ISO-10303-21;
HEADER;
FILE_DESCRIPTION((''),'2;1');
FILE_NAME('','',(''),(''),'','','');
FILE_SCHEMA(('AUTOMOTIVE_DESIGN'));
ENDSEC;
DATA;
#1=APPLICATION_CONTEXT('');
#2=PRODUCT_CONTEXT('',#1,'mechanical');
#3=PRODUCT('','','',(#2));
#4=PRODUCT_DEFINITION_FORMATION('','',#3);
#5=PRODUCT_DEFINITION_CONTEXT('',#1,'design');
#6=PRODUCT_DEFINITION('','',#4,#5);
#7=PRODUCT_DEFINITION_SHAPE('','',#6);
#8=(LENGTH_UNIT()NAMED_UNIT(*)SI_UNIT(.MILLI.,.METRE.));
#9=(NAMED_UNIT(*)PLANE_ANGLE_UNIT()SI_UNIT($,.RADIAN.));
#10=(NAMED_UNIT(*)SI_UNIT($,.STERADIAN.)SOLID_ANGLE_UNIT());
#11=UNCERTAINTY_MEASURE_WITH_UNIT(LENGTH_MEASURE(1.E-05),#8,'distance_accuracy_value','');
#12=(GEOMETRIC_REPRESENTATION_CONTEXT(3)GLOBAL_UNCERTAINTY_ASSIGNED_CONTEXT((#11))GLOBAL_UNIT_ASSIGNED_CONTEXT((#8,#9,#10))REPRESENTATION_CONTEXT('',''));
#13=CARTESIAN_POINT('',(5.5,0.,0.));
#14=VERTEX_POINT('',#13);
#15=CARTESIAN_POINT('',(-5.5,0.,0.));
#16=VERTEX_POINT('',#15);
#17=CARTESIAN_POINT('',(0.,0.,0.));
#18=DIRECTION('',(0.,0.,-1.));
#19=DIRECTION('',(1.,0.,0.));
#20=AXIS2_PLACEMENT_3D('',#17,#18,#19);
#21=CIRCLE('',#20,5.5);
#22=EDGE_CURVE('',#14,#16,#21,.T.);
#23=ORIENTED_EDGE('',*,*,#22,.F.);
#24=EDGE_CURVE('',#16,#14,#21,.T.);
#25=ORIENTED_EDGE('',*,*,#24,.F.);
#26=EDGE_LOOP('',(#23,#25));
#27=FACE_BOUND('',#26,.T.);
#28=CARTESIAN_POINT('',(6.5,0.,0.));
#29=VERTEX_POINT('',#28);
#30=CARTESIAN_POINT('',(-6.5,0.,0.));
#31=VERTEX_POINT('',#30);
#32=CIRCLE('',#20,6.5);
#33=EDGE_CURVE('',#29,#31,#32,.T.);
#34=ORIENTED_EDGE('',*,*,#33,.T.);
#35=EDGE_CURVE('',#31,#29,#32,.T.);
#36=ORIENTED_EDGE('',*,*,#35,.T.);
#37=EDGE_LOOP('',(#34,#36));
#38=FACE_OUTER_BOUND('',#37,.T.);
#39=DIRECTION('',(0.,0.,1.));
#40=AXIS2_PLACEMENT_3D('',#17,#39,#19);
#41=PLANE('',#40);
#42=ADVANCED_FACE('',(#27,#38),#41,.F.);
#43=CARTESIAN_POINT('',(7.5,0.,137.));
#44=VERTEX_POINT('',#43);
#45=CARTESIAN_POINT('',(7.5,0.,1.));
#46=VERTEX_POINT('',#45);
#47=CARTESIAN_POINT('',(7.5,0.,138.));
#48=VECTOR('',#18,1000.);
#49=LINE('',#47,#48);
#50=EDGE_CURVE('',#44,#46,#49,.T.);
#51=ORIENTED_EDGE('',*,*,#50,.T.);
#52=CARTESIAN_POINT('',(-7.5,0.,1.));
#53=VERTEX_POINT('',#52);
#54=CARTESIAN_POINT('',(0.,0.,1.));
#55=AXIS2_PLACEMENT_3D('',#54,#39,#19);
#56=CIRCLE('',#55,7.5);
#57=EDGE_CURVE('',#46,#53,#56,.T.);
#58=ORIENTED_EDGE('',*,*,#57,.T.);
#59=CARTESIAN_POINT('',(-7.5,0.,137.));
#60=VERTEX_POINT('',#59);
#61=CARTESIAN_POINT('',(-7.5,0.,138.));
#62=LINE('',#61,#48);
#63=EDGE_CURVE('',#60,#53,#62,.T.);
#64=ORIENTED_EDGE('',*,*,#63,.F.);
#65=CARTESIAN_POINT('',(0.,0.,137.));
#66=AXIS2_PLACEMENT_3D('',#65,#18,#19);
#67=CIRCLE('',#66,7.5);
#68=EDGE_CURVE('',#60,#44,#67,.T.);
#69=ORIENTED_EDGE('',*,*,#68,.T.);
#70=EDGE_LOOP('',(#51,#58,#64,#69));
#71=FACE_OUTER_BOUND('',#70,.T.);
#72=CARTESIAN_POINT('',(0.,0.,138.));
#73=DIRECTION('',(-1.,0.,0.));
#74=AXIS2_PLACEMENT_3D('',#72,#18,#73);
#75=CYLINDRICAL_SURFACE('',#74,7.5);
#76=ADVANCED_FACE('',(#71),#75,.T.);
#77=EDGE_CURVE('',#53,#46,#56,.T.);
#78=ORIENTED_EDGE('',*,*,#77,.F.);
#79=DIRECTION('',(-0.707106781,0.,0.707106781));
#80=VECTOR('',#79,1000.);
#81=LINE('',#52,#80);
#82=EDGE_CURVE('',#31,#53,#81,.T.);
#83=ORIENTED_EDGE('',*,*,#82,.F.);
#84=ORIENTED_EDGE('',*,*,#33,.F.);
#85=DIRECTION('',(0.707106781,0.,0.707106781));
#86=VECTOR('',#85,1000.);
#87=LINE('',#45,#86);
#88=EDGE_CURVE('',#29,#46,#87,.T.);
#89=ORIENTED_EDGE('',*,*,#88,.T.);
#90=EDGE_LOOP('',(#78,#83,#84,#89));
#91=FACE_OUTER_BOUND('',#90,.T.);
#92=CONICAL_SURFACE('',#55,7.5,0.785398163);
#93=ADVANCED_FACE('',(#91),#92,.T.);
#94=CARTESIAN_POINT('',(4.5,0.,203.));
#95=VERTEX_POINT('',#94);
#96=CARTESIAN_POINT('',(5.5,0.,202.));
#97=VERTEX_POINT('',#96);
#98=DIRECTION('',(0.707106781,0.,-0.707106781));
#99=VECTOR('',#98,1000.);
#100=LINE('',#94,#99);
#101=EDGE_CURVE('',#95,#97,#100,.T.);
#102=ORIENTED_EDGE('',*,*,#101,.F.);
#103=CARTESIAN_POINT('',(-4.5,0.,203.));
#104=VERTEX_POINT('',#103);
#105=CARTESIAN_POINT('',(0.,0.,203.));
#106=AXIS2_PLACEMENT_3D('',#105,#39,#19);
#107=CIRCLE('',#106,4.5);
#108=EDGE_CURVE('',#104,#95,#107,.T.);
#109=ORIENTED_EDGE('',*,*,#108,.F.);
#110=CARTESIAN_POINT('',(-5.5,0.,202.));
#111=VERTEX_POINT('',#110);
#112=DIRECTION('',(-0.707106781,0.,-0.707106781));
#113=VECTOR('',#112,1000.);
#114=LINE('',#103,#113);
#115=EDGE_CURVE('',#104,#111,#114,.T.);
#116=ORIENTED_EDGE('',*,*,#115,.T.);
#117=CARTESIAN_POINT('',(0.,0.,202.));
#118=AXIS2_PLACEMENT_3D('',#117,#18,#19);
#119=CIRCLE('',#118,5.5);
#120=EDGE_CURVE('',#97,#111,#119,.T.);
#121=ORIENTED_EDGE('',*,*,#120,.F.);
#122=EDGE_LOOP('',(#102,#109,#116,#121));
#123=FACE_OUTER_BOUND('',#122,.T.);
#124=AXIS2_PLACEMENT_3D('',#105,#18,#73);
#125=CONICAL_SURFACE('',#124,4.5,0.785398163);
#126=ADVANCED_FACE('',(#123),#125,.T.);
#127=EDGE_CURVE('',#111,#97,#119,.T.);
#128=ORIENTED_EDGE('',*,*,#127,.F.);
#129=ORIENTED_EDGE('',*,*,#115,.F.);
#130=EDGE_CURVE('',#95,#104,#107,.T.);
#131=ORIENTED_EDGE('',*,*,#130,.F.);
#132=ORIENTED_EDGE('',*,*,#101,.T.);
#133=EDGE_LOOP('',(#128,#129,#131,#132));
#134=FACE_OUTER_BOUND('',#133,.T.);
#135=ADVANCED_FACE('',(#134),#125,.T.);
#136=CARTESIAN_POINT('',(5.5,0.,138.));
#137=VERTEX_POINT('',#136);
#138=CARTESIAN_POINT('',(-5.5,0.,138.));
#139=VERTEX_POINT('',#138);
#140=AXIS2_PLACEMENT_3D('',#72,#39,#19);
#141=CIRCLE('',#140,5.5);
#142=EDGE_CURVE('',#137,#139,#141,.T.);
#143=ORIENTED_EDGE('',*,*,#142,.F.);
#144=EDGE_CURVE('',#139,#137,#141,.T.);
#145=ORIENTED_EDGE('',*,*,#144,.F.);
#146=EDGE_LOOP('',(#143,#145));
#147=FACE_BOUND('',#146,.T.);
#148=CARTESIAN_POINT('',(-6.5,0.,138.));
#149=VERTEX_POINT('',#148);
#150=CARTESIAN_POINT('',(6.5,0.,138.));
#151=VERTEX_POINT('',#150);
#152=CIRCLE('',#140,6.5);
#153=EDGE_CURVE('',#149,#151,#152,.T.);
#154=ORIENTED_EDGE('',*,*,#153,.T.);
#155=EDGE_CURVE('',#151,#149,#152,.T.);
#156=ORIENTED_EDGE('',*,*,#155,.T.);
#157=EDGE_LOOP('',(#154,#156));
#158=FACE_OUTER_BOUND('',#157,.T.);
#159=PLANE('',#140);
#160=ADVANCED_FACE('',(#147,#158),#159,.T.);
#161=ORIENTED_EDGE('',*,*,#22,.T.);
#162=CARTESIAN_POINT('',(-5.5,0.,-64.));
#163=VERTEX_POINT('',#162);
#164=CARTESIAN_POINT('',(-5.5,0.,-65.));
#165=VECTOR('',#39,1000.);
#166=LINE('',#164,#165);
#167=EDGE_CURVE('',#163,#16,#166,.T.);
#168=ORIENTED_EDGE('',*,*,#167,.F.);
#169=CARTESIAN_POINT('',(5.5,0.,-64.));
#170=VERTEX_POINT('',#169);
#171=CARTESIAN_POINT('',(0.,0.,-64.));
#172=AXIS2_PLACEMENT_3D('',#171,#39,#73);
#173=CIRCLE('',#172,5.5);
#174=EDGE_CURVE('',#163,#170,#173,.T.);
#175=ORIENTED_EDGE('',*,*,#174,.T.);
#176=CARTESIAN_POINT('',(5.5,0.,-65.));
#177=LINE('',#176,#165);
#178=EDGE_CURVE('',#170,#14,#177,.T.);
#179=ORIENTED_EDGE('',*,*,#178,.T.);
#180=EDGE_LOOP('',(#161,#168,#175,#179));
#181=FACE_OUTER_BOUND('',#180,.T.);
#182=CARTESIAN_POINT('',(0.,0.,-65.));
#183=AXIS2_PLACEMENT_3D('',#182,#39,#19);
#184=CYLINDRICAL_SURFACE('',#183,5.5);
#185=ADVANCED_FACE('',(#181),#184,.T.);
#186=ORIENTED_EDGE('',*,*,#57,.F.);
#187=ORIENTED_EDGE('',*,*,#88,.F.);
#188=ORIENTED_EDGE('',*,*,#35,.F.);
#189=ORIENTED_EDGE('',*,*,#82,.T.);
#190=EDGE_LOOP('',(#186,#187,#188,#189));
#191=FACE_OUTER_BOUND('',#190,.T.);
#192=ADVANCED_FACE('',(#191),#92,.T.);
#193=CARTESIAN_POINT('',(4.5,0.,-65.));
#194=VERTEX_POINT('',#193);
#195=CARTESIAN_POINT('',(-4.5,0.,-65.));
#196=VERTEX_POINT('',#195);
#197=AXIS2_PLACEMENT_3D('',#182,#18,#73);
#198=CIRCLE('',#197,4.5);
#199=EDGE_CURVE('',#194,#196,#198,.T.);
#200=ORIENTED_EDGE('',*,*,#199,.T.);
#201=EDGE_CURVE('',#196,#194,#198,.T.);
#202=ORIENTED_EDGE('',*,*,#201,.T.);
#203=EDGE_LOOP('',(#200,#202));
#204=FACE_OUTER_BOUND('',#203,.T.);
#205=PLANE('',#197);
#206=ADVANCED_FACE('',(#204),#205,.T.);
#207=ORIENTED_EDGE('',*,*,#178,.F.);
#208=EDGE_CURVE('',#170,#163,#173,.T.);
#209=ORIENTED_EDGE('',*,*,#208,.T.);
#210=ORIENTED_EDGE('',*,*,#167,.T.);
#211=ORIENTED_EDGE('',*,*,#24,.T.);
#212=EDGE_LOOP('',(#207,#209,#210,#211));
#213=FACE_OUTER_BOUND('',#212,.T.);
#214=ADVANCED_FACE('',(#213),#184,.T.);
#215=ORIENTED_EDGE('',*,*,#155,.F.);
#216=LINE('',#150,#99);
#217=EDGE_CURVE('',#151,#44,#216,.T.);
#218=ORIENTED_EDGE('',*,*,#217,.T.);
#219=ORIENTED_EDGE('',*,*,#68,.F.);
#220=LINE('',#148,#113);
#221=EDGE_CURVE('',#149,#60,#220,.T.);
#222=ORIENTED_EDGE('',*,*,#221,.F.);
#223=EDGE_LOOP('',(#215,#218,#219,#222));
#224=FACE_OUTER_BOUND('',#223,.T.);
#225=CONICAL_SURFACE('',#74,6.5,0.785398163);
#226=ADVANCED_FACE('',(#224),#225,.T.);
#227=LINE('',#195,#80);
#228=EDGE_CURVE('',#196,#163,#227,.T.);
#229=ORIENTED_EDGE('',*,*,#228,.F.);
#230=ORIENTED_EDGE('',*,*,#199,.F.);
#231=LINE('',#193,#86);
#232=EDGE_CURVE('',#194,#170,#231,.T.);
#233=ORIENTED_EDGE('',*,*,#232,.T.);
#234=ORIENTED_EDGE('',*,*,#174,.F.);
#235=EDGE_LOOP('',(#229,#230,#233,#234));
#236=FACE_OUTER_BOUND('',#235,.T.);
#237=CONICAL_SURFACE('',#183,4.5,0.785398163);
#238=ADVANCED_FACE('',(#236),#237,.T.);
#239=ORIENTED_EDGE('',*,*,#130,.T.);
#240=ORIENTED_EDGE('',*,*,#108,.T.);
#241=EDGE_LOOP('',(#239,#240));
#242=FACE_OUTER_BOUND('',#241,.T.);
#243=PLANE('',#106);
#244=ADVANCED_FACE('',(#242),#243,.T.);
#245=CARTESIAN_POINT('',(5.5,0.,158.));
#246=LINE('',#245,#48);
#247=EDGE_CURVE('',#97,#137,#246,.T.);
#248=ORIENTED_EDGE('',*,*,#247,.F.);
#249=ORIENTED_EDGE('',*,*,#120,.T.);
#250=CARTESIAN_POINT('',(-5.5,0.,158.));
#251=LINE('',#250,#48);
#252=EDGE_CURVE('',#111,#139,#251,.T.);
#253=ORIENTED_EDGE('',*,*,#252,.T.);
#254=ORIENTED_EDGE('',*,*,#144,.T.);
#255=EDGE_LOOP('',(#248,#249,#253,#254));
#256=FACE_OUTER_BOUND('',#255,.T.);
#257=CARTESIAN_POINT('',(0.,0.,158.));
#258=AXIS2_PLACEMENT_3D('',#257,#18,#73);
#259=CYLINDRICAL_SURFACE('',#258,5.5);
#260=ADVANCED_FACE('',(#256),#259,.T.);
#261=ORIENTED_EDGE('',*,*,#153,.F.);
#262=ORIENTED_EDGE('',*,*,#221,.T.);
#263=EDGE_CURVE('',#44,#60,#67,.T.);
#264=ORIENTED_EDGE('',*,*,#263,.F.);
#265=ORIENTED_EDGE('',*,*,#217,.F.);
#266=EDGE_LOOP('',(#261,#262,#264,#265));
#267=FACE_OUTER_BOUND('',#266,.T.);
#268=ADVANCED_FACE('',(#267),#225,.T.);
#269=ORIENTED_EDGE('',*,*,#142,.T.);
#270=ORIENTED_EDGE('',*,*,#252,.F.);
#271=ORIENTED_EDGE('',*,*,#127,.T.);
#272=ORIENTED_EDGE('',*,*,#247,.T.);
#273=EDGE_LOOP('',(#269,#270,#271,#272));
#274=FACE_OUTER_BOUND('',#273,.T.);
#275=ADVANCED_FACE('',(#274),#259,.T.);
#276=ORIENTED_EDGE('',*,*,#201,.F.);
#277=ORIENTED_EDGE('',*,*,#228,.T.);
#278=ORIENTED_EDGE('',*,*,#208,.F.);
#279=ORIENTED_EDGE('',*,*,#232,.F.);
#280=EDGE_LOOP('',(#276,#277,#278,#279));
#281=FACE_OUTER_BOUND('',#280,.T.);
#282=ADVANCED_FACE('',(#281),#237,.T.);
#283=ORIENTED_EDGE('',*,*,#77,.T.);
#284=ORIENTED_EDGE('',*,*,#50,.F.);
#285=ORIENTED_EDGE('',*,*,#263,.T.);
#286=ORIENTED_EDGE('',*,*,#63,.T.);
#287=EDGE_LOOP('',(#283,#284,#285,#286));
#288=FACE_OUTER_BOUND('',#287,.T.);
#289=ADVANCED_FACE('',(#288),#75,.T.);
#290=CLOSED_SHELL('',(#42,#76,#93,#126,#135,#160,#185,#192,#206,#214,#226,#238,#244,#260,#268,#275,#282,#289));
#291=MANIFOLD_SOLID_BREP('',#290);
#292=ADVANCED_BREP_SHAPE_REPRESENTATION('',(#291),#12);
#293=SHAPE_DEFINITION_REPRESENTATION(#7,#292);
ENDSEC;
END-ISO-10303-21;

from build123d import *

# Parameters (mm, degrees)
SKETCH1_R           = 7.5
BOSS_EXTRUDE1_DEPTH = 138
SKETCH2_R           = 5.5
BOSS_EXTRUDE2_DEPTH = 20
SKETCH3_R           = 5.5
BOSS_EXTRUDE3_DEPTH = 45
CHAMFER1_SIZE       = 1
BOSS_EXTRUDE4_START = 65
SKETCH4_R           = 5.5
BOSS_EXTRUDE4_DEPTH = 65
CHAMFER2_SIZE       = 1


with BuildPart() as part:
    # Sketch1 → Boss-Extrude1 (new body)
    with BuildSketch(Plane.XY):
        Circle(SKETCH1_R)
    extrude(amount=BOSS_EXTRUDE1_DEPTH)

    # Sketch2 → Boss-Extrude2 (add)
    with BuildSketch(Plane.XY.offset(138)):
        Circle(SKETCH2_R)
    extrude(amount=BOSS_EXTRUDE2_DEPTH)

    # Sketch3 → Boss-Extrude3 (add)
    with BuildSketch(Plane.XY.offset(158)):
        Circle(SKETCH3_R)
    extrude(amount=BOSS_EXTRUDE3_DEPTH)

    # Chamfer1
    chamfer1_edges = [part.edges().sort_by_distance(p)[0] for p in [
        (-7.5, 0, 0),
        (-7.5, 0, 138),
        (-5.5, 0, 203),
    ]]
    chamfer(chamfer1_edges, length=CHAMFER1_SIZE)

    # Sketch4 → Boss-Extrude4 (add)
    with BuildSketch(Plane(origin=(0, 0, 0), x_dir=(-1, 0, 0), z_dir=(0, 0, -1)).offset(BOSS_EXTRUDE4_START)):
        with Locations(Location((0, 0, 0), (0, 0, 180))):
            Circle(SKETCH4_R)
    extrude(amount=-BOSS_EXTRUDE4_DEPTH)

    # Chamfer2
    chamfer2_edges = [part.edges().sort_by_distance(p)[0] for p in [
        (-5.5, 0, -65),
    ]]
    chamfer(chamfer2_edges, length=CHAMFER2_SIZE)


solid = part.part
